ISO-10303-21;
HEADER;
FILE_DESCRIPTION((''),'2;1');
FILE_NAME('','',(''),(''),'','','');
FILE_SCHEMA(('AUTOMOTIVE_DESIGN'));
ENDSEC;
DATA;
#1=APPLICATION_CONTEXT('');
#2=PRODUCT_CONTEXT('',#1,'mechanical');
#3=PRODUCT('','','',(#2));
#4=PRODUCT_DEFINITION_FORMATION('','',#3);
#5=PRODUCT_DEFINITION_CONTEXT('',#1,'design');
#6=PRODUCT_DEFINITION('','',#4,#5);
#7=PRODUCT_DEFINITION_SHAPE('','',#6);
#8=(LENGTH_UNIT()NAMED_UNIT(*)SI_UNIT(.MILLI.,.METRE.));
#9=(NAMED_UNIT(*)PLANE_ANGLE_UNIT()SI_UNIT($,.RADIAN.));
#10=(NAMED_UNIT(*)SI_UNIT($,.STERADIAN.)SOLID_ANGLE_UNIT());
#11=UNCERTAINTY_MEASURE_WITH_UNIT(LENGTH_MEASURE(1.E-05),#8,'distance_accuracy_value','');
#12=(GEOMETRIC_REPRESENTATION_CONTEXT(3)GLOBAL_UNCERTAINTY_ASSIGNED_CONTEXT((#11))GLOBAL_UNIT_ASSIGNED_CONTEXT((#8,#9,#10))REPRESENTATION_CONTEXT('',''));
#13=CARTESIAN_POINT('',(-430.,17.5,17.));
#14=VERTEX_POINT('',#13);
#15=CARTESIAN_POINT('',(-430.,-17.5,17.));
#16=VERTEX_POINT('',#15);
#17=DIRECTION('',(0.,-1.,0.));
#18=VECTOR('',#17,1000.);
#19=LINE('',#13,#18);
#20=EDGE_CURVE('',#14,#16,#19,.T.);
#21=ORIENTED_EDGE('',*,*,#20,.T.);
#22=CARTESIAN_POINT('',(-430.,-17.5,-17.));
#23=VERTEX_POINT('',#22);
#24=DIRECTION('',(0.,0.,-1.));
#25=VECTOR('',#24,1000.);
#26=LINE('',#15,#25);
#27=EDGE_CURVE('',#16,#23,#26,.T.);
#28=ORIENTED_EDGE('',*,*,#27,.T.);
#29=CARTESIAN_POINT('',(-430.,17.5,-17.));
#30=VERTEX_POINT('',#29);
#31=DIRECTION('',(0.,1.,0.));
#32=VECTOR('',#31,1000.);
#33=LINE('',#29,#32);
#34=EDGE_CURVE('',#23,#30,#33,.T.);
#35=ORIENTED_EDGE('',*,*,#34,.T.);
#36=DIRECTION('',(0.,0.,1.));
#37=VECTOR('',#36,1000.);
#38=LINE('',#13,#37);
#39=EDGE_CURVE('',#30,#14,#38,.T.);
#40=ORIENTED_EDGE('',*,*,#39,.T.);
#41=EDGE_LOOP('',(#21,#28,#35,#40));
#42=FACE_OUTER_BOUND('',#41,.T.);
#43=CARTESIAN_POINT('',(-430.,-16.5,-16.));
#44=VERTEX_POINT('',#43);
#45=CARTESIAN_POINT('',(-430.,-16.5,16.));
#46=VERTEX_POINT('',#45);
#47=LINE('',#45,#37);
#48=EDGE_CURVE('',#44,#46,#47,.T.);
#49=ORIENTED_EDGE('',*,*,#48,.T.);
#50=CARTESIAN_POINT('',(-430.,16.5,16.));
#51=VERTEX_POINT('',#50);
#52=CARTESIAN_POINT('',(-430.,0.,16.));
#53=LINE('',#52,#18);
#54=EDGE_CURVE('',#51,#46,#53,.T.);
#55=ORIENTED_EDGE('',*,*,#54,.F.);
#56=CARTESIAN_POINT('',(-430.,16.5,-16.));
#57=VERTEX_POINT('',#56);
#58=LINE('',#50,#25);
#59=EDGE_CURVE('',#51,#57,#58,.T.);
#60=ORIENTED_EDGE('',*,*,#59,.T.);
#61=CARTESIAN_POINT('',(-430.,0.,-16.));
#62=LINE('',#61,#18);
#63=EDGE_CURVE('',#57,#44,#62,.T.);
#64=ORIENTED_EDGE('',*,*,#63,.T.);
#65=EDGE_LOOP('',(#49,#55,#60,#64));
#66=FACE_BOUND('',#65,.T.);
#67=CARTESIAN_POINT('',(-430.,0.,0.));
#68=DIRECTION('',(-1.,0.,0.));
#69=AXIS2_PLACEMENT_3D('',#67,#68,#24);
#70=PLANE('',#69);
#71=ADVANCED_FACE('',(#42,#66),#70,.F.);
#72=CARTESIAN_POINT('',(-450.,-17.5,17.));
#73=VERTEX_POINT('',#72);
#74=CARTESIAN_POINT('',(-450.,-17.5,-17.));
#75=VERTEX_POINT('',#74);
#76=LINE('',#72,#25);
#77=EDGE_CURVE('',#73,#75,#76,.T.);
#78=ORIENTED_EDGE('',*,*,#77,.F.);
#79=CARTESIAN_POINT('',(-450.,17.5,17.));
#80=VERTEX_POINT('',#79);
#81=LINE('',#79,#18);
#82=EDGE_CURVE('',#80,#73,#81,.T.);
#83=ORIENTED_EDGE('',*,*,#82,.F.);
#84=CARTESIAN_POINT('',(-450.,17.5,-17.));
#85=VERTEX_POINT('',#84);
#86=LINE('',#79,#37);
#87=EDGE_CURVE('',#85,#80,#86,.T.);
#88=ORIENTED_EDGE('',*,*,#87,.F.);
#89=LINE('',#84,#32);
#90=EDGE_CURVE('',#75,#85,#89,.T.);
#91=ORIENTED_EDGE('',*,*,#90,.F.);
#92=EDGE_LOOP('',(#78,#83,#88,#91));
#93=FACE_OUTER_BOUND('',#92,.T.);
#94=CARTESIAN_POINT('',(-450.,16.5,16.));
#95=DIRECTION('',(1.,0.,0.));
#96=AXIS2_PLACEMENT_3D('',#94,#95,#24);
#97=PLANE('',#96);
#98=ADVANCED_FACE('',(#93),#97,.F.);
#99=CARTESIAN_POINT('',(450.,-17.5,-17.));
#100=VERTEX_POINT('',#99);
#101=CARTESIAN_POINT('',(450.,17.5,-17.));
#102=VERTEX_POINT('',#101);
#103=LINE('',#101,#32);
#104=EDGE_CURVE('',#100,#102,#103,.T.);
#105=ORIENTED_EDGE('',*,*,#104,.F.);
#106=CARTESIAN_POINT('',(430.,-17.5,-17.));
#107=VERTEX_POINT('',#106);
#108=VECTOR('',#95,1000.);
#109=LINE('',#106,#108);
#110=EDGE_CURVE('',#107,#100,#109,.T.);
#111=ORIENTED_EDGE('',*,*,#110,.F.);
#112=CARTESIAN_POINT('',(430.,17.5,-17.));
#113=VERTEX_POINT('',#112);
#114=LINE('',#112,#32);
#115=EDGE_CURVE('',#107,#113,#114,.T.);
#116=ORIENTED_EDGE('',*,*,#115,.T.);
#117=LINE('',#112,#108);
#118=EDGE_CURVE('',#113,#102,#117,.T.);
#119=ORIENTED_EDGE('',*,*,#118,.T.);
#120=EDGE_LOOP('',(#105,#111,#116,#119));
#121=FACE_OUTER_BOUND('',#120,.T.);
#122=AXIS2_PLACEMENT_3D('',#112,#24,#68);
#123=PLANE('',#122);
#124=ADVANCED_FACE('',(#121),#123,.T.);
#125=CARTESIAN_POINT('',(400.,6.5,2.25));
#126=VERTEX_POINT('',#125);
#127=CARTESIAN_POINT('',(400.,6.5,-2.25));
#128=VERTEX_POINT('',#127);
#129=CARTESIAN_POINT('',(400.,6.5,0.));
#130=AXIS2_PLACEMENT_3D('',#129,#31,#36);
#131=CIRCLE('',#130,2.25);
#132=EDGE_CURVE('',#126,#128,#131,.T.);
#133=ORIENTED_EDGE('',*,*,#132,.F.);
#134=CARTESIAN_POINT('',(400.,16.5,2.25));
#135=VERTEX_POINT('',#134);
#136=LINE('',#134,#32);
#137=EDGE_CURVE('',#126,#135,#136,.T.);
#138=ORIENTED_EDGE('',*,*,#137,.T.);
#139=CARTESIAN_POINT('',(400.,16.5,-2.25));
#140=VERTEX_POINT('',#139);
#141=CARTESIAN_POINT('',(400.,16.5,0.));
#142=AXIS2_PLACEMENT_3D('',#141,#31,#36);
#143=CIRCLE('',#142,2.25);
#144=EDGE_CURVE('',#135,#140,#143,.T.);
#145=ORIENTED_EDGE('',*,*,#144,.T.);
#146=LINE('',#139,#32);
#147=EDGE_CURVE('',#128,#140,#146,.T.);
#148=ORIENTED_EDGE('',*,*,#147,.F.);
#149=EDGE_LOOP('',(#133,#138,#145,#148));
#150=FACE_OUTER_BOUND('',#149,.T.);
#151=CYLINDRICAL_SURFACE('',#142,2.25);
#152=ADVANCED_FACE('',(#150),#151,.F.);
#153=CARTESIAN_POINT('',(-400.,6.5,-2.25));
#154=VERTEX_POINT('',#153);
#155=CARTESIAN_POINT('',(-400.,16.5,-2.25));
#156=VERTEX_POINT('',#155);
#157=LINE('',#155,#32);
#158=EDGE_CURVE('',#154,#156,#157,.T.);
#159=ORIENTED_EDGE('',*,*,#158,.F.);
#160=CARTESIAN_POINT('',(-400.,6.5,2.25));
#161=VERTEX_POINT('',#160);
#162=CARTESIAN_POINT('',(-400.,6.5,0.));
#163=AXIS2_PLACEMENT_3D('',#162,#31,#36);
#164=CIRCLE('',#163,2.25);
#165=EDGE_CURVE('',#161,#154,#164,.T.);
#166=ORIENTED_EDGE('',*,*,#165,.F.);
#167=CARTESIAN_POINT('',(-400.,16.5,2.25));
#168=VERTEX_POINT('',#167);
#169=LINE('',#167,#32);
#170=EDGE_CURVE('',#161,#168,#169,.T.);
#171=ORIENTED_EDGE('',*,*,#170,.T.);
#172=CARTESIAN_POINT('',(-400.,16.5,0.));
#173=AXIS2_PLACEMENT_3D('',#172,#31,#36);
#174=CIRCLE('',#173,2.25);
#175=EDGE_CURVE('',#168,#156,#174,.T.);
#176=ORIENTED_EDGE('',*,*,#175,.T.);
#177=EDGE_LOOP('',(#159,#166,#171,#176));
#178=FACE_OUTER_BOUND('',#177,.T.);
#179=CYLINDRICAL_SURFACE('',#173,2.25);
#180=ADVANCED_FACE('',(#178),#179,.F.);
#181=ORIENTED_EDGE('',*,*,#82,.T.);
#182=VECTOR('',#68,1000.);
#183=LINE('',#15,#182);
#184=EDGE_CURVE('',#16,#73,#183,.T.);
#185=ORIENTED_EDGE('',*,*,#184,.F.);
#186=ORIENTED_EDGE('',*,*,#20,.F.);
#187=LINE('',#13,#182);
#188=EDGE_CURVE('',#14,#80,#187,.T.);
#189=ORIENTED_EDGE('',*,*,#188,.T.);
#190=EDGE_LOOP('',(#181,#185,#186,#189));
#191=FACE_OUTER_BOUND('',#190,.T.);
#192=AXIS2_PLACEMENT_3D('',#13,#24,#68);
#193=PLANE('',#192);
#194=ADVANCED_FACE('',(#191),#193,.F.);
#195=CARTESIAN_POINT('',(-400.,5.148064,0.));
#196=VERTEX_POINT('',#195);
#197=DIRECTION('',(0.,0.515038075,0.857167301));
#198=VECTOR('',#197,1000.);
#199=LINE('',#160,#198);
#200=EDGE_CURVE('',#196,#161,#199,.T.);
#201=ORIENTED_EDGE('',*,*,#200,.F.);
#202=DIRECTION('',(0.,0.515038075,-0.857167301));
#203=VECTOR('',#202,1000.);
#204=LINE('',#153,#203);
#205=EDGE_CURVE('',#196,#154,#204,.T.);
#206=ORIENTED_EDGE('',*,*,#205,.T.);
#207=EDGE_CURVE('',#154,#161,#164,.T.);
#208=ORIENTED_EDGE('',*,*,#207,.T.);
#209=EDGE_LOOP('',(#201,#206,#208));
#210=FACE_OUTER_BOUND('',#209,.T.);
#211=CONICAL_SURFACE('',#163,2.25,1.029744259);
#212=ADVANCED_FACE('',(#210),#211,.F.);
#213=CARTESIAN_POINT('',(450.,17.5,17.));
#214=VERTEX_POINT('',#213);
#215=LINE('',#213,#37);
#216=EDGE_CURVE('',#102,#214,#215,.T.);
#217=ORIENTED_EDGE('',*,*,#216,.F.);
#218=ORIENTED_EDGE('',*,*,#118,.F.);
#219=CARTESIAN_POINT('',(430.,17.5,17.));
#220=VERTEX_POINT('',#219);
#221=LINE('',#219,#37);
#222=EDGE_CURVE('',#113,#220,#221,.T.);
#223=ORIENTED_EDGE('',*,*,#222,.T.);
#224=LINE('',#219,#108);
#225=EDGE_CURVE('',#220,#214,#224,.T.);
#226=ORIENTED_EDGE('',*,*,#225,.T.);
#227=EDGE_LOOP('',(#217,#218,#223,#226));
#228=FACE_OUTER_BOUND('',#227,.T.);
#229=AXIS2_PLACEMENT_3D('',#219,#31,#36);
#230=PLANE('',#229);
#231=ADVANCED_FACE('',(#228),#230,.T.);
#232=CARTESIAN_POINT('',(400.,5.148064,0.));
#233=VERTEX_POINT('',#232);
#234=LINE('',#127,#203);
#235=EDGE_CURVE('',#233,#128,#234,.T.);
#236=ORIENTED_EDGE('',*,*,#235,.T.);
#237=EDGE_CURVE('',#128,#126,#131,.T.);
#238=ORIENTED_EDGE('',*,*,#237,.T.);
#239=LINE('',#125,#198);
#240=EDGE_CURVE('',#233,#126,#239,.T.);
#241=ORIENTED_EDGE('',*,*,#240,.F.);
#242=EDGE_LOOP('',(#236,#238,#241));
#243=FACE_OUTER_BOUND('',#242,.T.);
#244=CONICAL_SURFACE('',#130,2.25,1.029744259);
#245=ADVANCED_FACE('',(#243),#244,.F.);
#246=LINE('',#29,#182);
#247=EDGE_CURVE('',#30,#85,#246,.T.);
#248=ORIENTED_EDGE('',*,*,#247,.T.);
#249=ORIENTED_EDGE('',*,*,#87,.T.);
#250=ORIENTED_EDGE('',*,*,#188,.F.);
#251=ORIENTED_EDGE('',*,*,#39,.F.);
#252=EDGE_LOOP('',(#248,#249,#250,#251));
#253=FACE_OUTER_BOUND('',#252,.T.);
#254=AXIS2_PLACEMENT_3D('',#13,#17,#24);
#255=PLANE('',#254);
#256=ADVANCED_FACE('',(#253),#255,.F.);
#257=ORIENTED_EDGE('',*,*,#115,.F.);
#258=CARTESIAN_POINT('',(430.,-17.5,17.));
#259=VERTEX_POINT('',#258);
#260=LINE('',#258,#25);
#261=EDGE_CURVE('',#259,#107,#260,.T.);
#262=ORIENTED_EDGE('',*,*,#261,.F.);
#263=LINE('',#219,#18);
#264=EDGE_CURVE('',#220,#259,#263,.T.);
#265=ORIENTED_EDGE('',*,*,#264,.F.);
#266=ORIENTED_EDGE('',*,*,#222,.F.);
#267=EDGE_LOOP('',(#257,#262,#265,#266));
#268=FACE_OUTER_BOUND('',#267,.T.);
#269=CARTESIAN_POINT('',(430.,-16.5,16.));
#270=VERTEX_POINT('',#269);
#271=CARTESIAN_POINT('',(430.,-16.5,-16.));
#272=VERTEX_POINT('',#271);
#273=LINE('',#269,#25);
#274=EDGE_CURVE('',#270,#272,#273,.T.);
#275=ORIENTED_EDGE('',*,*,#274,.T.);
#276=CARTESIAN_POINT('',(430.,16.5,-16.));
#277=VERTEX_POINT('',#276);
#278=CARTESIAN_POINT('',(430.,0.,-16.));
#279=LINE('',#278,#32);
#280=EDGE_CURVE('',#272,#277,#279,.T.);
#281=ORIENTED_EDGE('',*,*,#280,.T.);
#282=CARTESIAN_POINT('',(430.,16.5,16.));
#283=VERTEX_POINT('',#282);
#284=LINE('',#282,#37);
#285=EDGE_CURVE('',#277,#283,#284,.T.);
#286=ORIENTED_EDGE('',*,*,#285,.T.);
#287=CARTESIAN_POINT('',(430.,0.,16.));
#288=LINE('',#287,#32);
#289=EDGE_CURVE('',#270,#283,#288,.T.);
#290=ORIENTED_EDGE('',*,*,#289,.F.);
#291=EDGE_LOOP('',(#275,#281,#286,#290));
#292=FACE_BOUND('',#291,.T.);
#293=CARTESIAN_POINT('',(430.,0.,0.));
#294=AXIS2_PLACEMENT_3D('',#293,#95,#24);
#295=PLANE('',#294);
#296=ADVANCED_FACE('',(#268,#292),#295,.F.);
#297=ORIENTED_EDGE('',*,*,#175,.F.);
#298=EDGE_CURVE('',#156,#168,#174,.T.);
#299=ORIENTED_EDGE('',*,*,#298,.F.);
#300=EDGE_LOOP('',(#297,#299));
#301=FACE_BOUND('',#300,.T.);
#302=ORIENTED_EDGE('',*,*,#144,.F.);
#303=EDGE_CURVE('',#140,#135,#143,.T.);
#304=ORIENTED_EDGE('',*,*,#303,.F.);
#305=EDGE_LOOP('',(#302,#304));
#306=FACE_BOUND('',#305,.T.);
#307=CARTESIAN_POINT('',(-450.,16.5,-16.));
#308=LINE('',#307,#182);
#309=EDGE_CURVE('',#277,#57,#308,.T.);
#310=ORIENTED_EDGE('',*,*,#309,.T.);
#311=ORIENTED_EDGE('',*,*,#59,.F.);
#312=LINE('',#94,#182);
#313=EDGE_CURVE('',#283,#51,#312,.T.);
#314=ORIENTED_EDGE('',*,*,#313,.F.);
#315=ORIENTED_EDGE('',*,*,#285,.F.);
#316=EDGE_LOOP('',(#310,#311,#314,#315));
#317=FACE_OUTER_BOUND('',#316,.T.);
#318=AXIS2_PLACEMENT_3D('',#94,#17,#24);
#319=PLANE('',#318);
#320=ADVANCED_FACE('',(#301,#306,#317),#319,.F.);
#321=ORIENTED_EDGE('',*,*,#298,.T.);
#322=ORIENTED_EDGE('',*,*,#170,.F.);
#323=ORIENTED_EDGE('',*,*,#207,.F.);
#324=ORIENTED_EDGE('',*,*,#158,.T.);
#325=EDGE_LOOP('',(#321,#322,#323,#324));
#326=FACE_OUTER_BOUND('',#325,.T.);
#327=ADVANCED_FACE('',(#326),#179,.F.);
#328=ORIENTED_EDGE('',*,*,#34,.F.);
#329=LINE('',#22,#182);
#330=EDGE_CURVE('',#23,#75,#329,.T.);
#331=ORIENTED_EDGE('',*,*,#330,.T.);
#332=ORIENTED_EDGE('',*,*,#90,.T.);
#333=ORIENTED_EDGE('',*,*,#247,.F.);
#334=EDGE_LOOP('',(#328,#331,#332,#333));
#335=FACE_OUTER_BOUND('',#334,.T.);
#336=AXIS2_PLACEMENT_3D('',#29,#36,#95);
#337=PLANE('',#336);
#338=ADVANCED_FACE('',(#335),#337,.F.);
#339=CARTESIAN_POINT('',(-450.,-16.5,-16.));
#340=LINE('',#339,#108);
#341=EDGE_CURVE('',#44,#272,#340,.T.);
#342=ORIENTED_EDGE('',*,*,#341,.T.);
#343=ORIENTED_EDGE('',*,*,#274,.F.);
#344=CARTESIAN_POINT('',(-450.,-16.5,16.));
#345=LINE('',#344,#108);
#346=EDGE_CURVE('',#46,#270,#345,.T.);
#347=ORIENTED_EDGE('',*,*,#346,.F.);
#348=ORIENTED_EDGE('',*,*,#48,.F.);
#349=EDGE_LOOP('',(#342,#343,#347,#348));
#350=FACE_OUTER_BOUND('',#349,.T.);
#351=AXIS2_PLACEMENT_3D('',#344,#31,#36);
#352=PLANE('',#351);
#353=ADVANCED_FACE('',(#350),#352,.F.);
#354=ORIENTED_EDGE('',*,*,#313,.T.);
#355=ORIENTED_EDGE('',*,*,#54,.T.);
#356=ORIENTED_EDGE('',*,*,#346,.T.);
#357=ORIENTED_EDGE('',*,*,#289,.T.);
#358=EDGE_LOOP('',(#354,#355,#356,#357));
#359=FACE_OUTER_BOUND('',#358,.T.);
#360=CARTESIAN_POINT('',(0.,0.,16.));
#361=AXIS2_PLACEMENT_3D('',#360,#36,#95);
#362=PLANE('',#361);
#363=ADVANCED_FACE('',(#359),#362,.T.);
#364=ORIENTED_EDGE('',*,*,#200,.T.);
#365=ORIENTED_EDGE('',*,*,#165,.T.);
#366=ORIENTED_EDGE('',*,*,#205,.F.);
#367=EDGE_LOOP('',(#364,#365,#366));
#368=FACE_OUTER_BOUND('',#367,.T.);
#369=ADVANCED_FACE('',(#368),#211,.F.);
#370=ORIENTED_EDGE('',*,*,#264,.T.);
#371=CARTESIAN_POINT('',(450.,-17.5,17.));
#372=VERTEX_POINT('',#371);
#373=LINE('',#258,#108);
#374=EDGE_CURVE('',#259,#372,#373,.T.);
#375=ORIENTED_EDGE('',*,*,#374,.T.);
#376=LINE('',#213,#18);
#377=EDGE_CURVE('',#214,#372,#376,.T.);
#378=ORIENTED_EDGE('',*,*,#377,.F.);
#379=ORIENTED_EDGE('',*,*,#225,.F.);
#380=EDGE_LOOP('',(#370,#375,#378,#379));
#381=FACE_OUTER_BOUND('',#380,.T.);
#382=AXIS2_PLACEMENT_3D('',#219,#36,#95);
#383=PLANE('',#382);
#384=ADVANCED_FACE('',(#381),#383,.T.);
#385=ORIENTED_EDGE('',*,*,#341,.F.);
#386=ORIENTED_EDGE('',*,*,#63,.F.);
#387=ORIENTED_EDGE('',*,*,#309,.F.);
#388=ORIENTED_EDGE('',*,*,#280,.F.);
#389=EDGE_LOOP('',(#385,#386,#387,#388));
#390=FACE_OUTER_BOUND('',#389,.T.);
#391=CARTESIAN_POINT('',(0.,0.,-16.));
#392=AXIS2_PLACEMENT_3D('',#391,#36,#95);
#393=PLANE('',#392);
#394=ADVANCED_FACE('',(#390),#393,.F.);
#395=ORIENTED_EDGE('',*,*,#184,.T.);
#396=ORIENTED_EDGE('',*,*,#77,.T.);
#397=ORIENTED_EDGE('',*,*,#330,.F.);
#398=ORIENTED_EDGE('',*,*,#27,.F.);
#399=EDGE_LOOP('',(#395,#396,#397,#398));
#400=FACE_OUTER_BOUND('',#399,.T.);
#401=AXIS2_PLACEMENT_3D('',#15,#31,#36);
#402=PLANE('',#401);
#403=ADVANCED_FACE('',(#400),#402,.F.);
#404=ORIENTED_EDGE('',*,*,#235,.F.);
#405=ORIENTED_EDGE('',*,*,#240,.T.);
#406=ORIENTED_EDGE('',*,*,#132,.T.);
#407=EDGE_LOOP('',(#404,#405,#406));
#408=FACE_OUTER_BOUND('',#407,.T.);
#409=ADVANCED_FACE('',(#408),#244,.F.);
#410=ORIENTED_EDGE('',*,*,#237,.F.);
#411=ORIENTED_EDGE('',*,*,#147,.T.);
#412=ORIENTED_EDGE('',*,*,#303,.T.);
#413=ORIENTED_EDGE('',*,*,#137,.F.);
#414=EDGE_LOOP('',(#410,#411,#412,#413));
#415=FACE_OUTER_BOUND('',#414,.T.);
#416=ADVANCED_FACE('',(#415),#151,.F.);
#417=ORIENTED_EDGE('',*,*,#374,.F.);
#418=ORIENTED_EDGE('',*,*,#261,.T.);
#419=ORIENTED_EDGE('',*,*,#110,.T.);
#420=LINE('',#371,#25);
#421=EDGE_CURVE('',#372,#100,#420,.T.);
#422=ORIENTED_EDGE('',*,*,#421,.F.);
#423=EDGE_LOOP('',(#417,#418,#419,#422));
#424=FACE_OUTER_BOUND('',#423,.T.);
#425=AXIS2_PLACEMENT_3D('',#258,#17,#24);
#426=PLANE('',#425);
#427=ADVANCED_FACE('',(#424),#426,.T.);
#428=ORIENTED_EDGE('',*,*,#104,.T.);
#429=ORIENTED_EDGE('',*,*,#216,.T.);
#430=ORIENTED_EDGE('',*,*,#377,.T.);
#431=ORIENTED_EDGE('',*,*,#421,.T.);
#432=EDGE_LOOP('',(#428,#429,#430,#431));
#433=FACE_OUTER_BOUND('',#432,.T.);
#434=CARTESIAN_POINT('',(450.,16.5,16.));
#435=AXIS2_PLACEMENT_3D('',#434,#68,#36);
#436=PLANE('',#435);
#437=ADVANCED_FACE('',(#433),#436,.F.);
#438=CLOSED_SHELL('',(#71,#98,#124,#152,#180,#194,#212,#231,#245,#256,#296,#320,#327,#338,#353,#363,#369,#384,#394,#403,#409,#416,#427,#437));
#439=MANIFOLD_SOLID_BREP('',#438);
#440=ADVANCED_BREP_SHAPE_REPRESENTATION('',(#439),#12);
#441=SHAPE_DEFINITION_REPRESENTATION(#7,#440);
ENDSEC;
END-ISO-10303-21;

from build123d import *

# Parameters (mm, degrees)
SKETCH_1_W                  = 900
SKETCH_1_H                  = 33
EXTRUDE_1_DEPTH             = 16
SKETCH_2_W                  = 34
SKETCH_2_H                  = 35
EXTRUDE_2_DEPTH             = 20
HOLE_WIZARD_4_5_4_5_1_D     = 4.5
HOLE_WIZARD_4_5_4_5_1_DEPTH = 10
HOLE_WIZARD_4_5_4_5_1_TIP   = 1.351936393


with BuildPart() as part:
    # 草图1 → 凸台-拉伸1 (new, symmetric)
    with BuildSketch(Plane.XY):
        Rectangle(SKETCH_1_W, SKETCH_1_H)
    extrude(amount=EXTRUDE_1_DEPTH, both=True)

    # 草图2 → 凸台-拉伸2 (add)
    with BuildSketch(Plane(origin=(450, 0, 0), x_dir=(0, 0, -1), z_dir=(1, 0, 0))):
        Rectangle(SKETCH_2_W, SKETCH_2_H)
    extrude_2 = extrude(amount=-EXTRUDE_2_DEPTH)

    # 镜向2: 凸台-拉伸2 across plane
    add(extrude_2.mirror(Plane(origin=(0, 0, 0), x_dir=(0, 0, 1), z_dir=(1, 0, 0))))

    # Ø4.5 (4.5) 直径孔1
    with Locations(Plane(origin=(0, 16.5, 0), x_dir=(1, 0, 0), z_dir=(0, 1, 0))):
        with Locations((-400, 0), (400, 0)):
            Hole(HOLE_WIZARD_4_5_4_5_1_D / 2, depth=HOLE_WIZARD_4_5_4_5_1_DEPTH)
            with Locations((0, 0, -(HOLE_WIZARD_4_5_4_5_1_DEPTH + HOLE_WIZARD_4_5_4_5_1_TIP / 2))):  # 118° drill point
                Cone(0, HOLE_WIZARD_4_5_4_5_1_D / 2, HOLE_WIZARD_4_5_4_5_1_TIP, mode=Mode.SUBTRACT)


solid = part.part
